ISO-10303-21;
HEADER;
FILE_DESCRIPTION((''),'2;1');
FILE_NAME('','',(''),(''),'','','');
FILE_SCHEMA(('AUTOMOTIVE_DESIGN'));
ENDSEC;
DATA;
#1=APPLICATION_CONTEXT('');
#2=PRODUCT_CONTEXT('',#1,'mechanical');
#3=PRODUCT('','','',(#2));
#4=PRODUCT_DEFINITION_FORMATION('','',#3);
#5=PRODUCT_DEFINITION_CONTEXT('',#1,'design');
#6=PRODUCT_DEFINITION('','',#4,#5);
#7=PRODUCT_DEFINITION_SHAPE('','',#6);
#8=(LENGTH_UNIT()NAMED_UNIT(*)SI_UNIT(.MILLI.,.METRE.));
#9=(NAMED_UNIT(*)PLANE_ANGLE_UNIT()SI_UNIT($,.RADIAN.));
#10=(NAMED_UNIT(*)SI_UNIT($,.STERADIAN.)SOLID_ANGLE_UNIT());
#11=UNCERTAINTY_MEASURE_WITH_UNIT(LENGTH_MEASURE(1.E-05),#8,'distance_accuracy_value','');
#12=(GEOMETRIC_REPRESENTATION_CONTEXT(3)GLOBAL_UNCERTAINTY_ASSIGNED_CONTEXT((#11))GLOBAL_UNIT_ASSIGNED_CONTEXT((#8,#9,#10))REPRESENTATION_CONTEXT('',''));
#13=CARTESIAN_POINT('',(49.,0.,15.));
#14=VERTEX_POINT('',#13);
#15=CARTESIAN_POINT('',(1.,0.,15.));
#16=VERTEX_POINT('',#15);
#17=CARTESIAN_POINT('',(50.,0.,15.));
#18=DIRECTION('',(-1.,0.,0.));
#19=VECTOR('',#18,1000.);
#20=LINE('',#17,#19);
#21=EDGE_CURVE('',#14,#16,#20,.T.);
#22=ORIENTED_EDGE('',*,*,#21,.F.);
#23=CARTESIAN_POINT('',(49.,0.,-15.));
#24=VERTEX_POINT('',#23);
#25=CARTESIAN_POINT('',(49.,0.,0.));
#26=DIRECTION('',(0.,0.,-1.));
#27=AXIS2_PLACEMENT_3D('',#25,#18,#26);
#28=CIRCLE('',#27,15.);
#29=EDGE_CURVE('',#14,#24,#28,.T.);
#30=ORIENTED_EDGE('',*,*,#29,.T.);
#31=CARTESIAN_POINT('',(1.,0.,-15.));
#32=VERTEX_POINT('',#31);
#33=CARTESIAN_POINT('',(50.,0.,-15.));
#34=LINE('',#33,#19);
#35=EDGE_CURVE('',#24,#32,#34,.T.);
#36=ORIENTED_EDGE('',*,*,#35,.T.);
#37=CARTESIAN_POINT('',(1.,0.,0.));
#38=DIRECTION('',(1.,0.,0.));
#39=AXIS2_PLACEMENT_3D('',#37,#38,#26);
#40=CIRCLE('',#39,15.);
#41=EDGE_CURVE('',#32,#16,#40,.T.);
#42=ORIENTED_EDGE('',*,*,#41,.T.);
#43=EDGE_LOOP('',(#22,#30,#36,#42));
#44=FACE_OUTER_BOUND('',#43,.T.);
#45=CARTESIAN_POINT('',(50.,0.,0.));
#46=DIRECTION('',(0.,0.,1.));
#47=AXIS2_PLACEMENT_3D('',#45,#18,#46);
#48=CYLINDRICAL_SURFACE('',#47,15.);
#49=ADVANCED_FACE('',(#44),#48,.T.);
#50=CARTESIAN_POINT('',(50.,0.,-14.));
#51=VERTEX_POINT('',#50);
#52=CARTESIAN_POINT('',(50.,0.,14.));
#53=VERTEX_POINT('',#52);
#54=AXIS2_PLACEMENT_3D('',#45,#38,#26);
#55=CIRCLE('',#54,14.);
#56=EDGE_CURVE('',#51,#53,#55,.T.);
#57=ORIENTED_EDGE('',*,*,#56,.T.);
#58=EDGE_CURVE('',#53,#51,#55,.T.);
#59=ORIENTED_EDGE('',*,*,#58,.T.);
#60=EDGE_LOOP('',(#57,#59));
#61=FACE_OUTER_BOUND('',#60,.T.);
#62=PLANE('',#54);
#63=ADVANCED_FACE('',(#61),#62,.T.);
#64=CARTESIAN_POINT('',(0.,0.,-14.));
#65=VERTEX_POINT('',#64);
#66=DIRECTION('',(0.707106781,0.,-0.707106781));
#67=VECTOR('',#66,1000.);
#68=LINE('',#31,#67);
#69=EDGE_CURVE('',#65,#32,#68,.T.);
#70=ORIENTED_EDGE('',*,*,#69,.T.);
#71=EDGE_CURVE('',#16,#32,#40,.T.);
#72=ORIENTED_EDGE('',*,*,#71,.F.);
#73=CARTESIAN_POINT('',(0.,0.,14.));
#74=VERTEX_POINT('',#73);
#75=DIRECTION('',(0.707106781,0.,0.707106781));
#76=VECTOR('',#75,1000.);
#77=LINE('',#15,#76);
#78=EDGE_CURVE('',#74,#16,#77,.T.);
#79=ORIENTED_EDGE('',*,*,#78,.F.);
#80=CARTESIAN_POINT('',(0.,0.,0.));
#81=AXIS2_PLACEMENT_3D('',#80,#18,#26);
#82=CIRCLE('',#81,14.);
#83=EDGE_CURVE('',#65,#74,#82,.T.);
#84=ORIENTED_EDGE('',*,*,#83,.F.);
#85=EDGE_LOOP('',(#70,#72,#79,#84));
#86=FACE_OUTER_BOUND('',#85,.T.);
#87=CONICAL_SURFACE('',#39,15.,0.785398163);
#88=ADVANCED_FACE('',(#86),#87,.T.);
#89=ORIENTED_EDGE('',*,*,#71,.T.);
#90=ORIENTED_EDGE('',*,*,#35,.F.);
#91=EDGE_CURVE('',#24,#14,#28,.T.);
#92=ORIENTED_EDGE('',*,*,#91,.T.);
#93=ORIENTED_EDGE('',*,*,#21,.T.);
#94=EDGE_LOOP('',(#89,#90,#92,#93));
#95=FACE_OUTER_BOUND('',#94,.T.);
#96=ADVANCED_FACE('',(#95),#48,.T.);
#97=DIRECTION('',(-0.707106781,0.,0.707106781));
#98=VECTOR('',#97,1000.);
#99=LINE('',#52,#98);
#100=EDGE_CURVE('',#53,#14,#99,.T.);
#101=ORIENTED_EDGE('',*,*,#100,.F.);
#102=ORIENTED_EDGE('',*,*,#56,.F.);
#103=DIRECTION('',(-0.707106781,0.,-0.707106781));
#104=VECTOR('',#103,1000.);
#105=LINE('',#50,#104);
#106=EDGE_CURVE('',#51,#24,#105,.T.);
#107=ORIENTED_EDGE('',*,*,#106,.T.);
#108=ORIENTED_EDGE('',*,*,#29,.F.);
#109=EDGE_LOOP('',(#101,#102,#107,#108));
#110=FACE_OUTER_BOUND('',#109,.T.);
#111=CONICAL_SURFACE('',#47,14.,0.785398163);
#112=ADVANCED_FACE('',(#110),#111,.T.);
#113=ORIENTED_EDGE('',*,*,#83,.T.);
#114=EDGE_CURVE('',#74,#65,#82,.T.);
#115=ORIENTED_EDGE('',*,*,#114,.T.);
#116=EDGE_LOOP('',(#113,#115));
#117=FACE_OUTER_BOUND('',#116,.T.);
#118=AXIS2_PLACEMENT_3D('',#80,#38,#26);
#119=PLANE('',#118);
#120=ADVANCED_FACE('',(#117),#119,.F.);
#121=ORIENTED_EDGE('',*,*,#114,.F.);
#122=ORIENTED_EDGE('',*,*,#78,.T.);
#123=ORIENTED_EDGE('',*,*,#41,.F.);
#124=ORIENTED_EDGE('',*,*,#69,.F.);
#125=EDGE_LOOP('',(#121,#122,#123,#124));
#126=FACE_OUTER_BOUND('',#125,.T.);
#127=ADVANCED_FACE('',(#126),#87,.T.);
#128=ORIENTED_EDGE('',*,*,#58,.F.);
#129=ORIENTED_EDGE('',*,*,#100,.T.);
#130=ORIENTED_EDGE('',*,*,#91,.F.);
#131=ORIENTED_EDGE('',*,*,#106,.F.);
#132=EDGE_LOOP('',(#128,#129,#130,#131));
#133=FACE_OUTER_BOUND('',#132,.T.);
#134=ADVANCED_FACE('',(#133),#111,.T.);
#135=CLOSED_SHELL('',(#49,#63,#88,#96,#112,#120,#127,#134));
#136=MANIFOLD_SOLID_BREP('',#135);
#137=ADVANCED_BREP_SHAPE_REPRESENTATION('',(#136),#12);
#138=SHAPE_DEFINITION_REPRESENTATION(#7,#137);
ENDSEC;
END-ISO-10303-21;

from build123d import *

# Parameters (mm, degrees)
SKETCH_1_R      = 15
EXTRUDE_1_DEPTH = 50
CHAMFER_1_SIZE  = 1


with BuildPart() as part:
    # 草图1 → 凸台-拉伸1 (new body)
    with BuildSketch(Plane(origin=(0, 0, 0), x_dir=(0, 0, -1), z_dir=(1, 0, 0))):
        Circle(SKETCH_1_R)
    extrude(amount=EXTRUDE_1_DEPTH)

    # 倒角1
    chamfer_1_edges = [part.edges().sort_by_distance(p)[0] for p in [
        (0, 0, 15),
        (50, 0, 15),
    ]]
    chamfer(chamfer_1_edges, length=CHAMFER_1_SIZE)


solid = part.part
